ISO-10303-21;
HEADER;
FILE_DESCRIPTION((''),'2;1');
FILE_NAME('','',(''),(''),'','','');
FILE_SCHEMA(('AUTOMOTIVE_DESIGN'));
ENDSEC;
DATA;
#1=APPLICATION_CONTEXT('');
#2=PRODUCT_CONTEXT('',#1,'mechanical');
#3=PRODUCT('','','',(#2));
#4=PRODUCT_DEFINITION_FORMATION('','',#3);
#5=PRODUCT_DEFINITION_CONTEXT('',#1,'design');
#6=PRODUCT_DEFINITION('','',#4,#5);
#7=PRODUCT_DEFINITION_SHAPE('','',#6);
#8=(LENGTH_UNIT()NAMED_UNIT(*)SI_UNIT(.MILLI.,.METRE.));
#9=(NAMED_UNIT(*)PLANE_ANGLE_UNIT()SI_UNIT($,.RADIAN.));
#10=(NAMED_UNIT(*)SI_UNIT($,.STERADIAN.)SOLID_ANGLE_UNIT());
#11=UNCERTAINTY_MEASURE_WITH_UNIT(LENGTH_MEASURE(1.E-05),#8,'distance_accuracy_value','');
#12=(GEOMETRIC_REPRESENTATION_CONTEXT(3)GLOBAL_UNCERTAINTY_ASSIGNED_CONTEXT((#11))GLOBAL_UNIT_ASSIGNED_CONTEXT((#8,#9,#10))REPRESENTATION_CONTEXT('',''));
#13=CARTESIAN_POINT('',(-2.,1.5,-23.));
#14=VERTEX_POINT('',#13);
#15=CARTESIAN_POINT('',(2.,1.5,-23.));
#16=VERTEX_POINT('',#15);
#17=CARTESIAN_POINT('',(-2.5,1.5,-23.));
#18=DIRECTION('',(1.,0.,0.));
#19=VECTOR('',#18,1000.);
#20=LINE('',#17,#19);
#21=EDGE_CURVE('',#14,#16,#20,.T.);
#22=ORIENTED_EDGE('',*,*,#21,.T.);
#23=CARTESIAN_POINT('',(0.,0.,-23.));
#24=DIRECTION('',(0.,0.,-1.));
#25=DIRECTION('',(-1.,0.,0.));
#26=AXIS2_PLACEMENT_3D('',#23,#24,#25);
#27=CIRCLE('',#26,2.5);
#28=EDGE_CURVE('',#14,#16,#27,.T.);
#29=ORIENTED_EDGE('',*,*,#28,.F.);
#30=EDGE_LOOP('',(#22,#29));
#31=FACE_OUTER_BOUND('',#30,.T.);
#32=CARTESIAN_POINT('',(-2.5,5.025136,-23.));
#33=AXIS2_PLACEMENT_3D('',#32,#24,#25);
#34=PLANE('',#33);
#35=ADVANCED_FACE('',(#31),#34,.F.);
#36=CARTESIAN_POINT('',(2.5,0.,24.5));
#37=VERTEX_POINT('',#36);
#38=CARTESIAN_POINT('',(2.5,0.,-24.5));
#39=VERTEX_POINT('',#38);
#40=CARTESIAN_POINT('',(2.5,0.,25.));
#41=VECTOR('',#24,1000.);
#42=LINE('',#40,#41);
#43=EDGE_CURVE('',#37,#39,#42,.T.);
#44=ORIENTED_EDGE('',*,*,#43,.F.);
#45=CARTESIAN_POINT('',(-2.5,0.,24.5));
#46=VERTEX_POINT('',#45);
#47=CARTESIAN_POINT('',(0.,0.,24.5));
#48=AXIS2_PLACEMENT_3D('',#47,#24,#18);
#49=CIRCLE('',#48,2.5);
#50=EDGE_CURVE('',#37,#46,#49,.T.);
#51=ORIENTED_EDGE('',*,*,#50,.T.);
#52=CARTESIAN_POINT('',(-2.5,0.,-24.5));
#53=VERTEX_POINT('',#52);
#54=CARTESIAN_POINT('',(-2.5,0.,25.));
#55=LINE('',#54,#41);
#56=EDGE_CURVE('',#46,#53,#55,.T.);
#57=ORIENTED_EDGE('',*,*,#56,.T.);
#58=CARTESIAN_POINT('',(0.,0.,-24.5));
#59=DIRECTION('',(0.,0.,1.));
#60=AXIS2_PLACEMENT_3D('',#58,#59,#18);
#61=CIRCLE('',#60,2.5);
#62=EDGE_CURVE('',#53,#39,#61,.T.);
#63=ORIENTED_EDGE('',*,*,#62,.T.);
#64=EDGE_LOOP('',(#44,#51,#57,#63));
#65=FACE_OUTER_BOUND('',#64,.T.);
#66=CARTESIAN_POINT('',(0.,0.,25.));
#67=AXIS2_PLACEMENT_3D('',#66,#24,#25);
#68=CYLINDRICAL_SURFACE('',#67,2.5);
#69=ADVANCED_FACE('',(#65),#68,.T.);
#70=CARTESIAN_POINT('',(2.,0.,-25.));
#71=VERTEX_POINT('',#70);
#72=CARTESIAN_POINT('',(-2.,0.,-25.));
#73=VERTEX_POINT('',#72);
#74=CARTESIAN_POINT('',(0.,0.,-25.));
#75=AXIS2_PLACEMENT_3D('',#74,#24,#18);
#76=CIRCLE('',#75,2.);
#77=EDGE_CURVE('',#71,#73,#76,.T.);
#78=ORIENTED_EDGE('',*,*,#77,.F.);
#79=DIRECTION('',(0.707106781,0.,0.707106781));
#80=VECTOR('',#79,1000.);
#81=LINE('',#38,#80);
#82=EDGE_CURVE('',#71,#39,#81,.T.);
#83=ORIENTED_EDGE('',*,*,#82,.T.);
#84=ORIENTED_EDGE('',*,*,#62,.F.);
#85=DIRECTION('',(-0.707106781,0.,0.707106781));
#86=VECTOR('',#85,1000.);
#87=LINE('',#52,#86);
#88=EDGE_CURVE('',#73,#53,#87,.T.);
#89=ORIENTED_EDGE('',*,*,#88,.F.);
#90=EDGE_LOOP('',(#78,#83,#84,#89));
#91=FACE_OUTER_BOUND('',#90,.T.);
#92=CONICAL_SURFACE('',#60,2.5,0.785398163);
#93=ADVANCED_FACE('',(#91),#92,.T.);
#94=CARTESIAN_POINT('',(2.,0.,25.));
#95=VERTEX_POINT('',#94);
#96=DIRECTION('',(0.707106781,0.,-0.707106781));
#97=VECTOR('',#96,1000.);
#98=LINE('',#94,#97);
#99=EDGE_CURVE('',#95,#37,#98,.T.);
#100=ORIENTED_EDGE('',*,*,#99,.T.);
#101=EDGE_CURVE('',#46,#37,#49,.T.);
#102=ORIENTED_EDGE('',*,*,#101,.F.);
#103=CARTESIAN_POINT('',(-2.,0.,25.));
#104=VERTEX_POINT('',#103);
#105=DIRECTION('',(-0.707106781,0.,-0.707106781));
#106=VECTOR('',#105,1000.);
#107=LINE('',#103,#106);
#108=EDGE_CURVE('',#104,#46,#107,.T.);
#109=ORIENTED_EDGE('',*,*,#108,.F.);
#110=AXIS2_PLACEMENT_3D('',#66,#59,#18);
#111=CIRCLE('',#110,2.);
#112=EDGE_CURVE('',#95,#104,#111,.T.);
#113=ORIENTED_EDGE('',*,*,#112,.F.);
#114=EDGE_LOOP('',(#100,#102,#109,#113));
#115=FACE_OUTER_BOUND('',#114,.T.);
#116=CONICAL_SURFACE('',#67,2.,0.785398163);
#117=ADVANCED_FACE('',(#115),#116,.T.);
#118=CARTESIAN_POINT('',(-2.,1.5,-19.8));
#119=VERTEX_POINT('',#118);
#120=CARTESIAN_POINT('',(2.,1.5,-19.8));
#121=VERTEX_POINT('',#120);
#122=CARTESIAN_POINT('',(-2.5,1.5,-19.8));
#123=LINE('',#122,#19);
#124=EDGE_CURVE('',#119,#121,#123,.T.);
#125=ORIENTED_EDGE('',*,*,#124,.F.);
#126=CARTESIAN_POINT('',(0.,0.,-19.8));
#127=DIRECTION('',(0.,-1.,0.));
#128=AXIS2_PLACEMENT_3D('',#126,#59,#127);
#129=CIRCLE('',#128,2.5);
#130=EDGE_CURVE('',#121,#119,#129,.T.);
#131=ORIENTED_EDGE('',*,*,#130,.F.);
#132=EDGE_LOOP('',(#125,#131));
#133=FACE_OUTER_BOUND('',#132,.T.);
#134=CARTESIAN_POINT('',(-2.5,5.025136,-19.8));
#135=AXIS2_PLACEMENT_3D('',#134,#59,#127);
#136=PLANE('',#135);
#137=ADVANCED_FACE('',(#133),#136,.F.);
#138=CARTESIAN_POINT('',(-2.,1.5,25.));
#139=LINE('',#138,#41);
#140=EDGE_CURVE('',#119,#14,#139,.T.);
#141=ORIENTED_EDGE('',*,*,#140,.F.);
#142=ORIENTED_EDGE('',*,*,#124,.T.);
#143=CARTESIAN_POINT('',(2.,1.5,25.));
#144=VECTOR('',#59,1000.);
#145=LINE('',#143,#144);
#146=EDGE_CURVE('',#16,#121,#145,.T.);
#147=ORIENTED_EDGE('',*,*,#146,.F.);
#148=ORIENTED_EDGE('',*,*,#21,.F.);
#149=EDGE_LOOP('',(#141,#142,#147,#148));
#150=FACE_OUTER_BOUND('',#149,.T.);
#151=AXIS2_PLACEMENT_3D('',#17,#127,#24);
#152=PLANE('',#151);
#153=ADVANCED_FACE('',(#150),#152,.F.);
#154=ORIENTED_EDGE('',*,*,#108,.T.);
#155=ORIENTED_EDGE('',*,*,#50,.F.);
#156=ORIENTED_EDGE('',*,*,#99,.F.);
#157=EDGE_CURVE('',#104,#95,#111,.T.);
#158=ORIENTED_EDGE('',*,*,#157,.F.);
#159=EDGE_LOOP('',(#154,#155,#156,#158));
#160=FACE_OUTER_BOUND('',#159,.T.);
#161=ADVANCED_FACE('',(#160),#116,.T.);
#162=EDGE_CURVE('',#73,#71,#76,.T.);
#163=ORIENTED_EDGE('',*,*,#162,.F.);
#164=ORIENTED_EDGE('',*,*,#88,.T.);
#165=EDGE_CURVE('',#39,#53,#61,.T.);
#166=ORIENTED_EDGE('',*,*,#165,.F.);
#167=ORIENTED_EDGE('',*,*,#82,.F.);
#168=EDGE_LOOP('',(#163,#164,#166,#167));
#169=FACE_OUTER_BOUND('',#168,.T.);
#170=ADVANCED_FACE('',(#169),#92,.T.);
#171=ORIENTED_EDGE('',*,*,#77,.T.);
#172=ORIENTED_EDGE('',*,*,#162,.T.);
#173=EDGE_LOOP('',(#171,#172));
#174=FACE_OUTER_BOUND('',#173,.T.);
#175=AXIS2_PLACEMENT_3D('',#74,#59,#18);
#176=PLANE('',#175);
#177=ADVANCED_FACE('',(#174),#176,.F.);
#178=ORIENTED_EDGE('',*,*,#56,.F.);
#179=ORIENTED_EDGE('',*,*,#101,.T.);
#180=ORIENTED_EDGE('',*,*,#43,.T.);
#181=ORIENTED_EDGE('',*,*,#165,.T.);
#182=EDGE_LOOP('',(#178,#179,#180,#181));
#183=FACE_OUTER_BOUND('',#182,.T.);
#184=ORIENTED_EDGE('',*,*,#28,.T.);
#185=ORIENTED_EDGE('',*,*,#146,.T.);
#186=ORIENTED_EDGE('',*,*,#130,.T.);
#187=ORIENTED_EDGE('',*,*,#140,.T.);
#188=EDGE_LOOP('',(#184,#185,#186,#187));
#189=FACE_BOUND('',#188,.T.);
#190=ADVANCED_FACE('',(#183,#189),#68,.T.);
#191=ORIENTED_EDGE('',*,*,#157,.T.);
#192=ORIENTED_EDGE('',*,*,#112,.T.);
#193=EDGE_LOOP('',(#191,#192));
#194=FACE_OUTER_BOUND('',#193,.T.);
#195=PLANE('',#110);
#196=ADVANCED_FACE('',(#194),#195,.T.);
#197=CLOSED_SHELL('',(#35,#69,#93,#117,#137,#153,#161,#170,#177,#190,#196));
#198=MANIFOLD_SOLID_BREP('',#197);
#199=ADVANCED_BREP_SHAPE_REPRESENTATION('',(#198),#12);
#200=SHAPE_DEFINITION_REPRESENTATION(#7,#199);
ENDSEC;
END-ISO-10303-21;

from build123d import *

# Parameters (mm, degrees)
SKETCH_1_R               = 2.5
EXTRUDE_1_DEPTH          = 25
CHAMFER_1_SIZE           = 0.5
CUT_EXTRUDE_1_DEPTH      = 26.248762346
CUT_EXTRUDE_1_DEPTH_BACK = 26.248762346
SKETCH_2_W               = 3.2
SKETCH_2_H               = 3.525136196


with BuildPart() as part:
    # 草图1 → 凸台-拉伸1 (new, symmetric)
    with BuildSketch(Plane.XY):
        Circle(SKETCH_1_R)
    extrude(amount=EXTRUDE_1_DEPTH, both=True)

    # 倒角1
    chamfer_1_edges = [part.edges().sort_by_distance(p)[0] for p in [
        (-2.5, 0, -25),
        (-2.5, 0, 25),
    ]]
    chamfer(chamfer_1_edges, length=CHAMFER_1_SIZE)

    # 草图2 → 切除-拉伸1 (cut, two sides: drawn at the far end of the back side and taken through both)
    with BuildSketch(Plane(origin=(0, 0, 0), x_dir=(0, 0, -1), z_dir=(1, 0, 0)).offset(-CUT_EXTRUDE_1_DEPTH_BACK)):
        with Locations((21.4, 3.262568098)):
            Rectangle(SKETCH_2_W, SKETCH_2_H)
    extrude(amount=CUT_EXTRUDE_1_DEPTH + CUT_EXTRUDE_1_DEPTH_BACK, mode=Mode.SUBTRACT)


solid = part.part
